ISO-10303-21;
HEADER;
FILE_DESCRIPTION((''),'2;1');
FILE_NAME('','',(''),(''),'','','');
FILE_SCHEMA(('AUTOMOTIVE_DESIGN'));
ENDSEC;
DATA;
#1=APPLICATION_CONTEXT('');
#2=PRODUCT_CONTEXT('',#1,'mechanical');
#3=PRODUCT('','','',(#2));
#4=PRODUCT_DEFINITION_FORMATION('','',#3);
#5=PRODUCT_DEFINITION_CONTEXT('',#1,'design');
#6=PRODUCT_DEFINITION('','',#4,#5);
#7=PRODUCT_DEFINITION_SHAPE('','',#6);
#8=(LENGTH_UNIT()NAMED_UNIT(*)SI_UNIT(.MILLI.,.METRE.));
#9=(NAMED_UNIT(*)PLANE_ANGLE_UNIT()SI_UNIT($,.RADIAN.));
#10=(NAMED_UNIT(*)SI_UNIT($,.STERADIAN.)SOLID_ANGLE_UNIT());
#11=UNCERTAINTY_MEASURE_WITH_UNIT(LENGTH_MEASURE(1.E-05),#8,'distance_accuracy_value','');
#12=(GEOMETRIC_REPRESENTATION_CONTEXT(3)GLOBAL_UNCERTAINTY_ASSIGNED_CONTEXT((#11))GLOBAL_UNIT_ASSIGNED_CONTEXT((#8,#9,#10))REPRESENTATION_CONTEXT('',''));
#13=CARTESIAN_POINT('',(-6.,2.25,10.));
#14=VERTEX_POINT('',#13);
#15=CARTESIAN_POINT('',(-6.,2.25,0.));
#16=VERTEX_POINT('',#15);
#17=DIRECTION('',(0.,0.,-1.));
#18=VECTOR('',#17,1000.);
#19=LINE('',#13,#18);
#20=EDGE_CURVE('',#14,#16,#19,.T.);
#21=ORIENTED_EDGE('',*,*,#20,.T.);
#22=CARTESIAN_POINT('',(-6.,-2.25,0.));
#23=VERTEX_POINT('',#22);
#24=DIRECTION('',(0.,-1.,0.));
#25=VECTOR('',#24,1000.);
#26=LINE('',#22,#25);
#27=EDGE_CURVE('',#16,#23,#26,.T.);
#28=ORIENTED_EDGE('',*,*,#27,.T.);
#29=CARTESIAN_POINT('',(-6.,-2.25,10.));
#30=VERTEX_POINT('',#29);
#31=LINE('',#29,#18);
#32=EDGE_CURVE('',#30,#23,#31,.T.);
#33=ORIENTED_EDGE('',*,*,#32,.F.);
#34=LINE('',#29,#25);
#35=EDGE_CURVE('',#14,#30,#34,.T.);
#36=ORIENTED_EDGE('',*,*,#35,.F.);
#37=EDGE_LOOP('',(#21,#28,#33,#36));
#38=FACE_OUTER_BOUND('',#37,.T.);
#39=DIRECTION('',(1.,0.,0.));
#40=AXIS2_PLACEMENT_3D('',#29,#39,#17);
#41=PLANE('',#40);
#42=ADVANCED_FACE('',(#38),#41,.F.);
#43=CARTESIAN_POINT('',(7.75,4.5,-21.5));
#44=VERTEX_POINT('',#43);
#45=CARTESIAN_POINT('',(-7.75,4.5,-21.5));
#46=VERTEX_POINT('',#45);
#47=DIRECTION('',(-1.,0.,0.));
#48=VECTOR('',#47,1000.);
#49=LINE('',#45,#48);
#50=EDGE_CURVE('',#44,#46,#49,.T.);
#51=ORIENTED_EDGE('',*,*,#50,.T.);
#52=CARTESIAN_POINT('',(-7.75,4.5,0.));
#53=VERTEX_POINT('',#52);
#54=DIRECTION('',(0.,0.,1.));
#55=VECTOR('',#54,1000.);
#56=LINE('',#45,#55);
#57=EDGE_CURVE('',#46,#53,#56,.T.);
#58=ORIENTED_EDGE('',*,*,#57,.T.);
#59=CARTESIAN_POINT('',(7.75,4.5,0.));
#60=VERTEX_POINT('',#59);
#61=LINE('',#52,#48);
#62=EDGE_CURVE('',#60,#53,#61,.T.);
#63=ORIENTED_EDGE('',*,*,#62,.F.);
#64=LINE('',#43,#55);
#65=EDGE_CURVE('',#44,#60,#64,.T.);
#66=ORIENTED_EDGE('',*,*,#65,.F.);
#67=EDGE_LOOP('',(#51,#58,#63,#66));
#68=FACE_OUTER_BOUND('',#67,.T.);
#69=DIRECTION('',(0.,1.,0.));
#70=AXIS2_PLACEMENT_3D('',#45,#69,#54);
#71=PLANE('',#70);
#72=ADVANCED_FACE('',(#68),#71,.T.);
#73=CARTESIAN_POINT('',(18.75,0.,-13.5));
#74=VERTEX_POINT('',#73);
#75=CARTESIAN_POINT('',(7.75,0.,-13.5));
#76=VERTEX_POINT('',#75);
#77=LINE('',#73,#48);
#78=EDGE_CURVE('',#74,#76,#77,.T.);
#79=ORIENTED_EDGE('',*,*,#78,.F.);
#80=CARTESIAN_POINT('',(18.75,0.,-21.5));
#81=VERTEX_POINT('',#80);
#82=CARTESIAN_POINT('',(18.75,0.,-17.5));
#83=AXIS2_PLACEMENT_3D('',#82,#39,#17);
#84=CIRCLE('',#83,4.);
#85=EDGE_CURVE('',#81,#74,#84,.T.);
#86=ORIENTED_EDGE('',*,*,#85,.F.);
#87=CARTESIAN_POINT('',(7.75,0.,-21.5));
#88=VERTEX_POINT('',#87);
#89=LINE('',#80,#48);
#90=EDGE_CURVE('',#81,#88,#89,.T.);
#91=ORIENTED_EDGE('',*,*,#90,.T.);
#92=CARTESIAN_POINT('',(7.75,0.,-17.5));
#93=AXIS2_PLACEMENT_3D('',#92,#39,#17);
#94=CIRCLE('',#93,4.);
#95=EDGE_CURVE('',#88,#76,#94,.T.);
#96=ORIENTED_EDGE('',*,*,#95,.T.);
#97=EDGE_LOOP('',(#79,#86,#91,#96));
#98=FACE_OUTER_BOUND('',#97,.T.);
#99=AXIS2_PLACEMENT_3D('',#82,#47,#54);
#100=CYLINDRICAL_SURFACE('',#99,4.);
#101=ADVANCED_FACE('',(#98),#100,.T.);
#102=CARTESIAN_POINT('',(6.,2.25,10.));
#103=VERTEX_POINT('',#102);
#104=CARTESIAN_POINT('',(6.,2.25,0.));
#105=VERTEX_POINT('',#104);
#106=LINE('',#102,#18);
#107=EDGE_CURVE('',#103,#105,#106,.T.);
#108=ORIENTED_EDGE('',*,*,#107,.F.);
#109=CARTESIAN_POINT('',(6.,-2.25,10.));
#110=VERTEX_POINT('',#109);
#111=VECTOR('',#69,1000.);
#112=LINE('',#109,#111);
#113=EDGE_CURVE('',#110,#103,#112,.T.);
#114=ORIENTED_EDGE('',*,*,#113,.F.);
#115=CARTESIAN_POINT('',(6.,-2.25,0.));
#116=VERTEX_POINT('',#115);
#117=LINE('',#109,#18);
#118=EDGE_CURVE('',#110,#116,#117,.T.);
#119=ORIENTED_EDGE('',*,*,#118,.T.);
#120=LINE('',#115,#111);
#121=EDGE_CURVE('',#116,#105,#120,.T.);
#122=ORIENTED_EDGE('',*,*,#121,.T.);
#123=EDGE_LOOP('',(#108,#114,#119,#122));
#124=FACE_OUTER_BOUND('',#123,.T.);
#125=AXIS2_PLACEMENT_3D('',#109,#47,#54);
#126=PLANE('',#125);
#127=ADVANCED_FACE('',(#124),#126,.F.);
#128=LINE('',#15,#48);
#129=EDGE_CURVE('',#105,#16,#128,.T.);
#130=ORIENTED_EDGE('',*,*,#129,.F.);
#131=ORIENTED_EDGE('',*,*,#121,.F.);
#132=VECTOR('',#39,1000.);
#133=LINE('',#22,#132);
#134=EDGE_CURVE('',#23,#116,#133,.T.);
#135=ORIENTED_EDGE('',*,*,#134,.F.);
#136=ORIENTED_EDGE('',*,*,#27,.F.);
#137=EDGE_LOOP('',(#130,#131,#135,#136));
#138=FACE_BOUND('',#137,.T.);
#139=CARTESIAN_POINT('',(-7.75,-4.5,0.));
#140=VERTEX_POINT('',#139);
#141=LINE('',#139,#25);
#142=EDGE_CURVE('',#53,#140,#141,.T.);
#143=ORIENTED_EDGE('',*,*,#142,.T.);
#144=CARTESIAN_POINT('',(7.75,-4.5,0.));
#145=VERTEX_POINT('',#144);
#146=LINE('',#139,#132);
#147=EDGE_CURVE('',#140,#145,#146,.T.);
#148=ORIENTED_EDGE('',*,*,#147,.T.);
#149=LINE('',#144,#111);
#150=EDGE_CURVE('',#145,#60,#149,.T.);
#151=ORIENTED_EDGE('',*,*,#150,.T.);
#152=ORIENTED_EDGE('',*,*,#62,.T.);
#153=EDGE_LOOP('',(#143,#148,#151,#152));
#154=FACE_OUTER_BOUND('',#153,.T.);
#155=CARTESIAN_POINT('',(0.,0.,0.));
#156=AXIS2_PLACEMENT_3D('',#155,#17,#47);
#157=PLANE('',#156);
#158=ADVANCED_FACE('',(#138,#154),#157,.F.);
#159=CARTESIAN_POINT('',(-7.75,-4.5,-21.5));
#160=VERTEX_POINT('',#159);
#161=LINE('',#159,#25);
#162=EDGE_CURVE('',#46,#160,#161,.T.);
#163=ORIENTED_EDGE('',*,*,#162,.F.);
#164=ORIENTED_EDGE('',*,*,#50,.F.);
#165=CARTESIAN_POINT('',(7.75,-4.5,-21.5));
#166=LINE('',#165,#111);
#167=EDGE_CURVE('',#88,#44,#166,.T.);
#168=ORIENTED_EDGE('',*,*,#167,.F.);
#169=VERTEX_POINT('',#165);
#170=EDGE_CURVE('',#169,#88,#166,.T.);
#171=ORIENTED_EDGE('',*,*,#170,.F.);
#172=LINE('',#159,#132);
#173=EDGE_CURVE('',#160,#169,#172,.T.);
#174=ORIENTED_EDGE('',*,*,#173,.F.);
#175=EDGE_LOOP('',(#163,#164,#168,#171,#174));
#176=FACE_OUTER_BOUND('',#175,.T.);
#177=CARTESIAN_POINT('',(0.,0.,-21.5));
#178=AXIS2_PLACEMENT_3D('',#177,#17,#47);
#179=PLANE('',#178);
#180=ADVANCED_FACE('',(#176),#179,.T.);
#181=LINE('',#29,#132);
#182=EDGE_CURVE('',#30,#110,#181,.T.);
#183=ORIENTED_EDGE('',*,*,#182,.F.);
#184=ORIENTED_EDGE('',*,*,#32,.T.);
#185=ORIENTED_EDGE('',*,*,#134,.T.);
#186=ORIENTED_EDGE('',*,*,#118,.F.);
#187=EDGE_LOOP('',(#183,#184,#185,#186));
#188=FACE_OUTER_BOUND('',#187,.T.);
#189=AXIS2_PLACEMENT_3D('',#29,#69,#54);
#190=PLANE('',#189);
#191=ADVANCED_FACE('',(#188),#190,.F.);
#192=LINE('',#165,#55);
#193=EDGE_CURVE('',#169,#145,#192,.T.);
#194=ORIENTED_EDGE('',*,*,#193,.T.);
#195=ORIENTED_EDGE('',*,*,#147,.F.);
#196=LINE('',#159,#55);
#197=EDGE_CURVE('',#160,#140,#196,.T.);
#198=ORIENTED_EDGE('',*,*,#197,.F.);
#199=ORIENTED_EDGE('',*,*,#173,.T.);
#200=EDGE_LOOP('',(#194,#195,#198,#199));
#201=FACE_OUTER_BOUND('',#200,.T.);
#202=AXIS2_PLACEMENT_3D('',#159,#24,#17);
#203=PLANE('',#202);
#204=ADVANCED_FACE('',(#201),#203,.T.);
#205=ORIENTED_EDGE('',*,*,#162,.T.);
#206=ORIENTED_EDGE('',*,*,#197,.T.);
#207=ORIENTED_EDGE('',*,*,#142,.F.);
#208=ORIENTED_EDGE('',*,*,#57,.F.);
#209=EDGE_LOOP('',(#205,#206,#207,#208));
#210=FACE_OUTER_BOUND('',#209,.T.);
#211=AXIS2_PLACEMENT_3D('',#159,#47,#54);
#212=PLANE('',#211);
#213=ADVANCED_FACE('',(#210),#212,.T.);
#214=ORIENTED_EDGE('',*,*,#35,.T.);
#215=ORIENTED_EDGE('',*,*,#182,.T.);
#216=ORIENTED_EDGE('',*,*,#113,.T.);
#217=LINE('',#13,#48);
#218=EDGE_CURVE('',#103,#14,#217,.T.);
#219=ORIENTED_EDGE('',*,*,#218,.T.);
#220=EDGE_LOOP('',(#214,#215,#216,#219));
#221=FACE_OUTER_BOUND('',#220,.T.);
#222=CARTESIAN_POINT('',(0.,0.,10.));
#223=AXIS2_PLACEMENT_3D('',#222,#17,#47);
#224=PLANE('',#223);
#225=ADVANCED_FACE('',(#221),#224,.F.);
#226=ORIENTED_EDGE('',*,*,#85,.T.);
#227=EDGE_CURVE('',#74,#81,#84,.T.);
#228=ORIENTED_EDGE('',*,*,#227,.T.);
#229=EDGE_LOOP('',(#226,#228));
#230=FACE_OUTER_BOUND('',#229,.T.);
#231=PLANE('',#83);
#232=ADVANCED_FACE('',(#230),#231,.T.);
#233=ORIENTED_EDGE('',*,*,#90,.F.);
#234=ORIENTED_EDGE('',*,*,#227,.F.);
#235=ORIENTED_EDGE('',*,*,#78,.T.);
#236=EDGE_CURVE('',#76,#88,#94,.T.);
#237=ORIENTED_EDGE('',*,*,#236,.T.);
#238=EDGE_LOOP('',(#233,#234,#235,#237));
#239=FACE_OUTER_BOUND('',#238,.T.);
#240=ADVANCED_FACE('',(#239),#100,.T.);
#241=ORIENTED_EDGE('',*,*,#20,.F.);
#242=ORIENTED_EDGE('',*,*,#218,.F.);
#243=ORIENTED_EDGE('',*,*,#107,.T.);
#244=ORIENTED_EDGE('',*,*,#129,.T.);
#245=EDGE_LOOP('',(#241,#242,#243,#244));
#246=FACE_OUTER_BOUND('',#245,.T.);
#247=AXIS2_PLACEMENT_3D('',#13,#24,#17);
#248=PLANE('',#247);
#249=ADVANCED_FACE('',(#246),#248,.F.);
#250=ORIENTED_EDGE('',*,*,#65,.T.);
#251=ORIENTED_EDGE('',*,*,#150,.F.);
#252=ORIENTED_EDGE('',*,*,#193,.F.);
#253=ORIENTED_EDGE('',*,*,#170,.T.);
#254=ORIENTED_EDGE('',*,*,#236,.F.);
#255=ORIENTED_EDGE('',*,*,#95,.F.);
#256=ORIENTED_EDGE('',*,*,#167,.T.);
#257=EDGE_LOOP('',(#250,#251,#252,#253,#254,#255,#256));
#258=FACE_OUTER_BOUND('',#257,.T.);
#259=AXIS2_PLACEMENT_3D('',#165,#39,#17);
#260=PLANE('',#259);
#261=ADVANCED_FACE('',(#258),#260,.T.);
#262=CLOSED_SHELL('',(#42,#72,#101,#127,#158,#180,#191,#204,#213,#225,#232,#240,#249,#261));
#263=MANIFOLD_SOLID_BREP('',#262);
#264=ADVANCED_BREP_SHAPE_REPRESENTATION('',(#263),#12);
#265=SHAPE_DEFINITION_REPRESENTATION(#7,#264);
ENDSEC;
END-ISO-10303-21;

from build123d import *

# Parameters (mm, degrees)
SKETCH1_W           = 15.5
SKETCH1_H           = 9
BOSS_EXTRUDE1_DEPTH = 21.5
SKETCH2_R           = 4
BOSS_EXTRUDE2_DEPTH = 11
SKETCH3_W           = 12
SKETCH3_H           = 4.5
BOSS_EXTRUDE3_DEPTH = 10


with BuildPart() as part:
    # Sketch1 → Boss-Extrude1 (new body)
    with BuildSketch(Plane.XY):
        Rectangle(SKETCH1_W, SKETCH1_H)
    extrude(amount=-BOSS_EXTRUDE1_DEPTH)

    # Sketch2 → Boss-Extrude2 (add)
    with BuildSketch(Plane(origin=(7.75, 0, 0), x_dir=(0, 0, -1), z_dir=(1, 0, 0))):
        with Locations((17.5, 0)):
            Circle(SKETCH2_R)
    extrude(amount=BOSS_EXTRUDE2_DEPTH)

    # Sketch3 → Boss-Extrude3 (add)
    with BuildSketch(Plane.XY):
        Rectangle(SKETCH3_W, SKETCH3_H)
    extrude(amount=BOSS_EXTRUDE3_DEPTH)


solid = part.part
